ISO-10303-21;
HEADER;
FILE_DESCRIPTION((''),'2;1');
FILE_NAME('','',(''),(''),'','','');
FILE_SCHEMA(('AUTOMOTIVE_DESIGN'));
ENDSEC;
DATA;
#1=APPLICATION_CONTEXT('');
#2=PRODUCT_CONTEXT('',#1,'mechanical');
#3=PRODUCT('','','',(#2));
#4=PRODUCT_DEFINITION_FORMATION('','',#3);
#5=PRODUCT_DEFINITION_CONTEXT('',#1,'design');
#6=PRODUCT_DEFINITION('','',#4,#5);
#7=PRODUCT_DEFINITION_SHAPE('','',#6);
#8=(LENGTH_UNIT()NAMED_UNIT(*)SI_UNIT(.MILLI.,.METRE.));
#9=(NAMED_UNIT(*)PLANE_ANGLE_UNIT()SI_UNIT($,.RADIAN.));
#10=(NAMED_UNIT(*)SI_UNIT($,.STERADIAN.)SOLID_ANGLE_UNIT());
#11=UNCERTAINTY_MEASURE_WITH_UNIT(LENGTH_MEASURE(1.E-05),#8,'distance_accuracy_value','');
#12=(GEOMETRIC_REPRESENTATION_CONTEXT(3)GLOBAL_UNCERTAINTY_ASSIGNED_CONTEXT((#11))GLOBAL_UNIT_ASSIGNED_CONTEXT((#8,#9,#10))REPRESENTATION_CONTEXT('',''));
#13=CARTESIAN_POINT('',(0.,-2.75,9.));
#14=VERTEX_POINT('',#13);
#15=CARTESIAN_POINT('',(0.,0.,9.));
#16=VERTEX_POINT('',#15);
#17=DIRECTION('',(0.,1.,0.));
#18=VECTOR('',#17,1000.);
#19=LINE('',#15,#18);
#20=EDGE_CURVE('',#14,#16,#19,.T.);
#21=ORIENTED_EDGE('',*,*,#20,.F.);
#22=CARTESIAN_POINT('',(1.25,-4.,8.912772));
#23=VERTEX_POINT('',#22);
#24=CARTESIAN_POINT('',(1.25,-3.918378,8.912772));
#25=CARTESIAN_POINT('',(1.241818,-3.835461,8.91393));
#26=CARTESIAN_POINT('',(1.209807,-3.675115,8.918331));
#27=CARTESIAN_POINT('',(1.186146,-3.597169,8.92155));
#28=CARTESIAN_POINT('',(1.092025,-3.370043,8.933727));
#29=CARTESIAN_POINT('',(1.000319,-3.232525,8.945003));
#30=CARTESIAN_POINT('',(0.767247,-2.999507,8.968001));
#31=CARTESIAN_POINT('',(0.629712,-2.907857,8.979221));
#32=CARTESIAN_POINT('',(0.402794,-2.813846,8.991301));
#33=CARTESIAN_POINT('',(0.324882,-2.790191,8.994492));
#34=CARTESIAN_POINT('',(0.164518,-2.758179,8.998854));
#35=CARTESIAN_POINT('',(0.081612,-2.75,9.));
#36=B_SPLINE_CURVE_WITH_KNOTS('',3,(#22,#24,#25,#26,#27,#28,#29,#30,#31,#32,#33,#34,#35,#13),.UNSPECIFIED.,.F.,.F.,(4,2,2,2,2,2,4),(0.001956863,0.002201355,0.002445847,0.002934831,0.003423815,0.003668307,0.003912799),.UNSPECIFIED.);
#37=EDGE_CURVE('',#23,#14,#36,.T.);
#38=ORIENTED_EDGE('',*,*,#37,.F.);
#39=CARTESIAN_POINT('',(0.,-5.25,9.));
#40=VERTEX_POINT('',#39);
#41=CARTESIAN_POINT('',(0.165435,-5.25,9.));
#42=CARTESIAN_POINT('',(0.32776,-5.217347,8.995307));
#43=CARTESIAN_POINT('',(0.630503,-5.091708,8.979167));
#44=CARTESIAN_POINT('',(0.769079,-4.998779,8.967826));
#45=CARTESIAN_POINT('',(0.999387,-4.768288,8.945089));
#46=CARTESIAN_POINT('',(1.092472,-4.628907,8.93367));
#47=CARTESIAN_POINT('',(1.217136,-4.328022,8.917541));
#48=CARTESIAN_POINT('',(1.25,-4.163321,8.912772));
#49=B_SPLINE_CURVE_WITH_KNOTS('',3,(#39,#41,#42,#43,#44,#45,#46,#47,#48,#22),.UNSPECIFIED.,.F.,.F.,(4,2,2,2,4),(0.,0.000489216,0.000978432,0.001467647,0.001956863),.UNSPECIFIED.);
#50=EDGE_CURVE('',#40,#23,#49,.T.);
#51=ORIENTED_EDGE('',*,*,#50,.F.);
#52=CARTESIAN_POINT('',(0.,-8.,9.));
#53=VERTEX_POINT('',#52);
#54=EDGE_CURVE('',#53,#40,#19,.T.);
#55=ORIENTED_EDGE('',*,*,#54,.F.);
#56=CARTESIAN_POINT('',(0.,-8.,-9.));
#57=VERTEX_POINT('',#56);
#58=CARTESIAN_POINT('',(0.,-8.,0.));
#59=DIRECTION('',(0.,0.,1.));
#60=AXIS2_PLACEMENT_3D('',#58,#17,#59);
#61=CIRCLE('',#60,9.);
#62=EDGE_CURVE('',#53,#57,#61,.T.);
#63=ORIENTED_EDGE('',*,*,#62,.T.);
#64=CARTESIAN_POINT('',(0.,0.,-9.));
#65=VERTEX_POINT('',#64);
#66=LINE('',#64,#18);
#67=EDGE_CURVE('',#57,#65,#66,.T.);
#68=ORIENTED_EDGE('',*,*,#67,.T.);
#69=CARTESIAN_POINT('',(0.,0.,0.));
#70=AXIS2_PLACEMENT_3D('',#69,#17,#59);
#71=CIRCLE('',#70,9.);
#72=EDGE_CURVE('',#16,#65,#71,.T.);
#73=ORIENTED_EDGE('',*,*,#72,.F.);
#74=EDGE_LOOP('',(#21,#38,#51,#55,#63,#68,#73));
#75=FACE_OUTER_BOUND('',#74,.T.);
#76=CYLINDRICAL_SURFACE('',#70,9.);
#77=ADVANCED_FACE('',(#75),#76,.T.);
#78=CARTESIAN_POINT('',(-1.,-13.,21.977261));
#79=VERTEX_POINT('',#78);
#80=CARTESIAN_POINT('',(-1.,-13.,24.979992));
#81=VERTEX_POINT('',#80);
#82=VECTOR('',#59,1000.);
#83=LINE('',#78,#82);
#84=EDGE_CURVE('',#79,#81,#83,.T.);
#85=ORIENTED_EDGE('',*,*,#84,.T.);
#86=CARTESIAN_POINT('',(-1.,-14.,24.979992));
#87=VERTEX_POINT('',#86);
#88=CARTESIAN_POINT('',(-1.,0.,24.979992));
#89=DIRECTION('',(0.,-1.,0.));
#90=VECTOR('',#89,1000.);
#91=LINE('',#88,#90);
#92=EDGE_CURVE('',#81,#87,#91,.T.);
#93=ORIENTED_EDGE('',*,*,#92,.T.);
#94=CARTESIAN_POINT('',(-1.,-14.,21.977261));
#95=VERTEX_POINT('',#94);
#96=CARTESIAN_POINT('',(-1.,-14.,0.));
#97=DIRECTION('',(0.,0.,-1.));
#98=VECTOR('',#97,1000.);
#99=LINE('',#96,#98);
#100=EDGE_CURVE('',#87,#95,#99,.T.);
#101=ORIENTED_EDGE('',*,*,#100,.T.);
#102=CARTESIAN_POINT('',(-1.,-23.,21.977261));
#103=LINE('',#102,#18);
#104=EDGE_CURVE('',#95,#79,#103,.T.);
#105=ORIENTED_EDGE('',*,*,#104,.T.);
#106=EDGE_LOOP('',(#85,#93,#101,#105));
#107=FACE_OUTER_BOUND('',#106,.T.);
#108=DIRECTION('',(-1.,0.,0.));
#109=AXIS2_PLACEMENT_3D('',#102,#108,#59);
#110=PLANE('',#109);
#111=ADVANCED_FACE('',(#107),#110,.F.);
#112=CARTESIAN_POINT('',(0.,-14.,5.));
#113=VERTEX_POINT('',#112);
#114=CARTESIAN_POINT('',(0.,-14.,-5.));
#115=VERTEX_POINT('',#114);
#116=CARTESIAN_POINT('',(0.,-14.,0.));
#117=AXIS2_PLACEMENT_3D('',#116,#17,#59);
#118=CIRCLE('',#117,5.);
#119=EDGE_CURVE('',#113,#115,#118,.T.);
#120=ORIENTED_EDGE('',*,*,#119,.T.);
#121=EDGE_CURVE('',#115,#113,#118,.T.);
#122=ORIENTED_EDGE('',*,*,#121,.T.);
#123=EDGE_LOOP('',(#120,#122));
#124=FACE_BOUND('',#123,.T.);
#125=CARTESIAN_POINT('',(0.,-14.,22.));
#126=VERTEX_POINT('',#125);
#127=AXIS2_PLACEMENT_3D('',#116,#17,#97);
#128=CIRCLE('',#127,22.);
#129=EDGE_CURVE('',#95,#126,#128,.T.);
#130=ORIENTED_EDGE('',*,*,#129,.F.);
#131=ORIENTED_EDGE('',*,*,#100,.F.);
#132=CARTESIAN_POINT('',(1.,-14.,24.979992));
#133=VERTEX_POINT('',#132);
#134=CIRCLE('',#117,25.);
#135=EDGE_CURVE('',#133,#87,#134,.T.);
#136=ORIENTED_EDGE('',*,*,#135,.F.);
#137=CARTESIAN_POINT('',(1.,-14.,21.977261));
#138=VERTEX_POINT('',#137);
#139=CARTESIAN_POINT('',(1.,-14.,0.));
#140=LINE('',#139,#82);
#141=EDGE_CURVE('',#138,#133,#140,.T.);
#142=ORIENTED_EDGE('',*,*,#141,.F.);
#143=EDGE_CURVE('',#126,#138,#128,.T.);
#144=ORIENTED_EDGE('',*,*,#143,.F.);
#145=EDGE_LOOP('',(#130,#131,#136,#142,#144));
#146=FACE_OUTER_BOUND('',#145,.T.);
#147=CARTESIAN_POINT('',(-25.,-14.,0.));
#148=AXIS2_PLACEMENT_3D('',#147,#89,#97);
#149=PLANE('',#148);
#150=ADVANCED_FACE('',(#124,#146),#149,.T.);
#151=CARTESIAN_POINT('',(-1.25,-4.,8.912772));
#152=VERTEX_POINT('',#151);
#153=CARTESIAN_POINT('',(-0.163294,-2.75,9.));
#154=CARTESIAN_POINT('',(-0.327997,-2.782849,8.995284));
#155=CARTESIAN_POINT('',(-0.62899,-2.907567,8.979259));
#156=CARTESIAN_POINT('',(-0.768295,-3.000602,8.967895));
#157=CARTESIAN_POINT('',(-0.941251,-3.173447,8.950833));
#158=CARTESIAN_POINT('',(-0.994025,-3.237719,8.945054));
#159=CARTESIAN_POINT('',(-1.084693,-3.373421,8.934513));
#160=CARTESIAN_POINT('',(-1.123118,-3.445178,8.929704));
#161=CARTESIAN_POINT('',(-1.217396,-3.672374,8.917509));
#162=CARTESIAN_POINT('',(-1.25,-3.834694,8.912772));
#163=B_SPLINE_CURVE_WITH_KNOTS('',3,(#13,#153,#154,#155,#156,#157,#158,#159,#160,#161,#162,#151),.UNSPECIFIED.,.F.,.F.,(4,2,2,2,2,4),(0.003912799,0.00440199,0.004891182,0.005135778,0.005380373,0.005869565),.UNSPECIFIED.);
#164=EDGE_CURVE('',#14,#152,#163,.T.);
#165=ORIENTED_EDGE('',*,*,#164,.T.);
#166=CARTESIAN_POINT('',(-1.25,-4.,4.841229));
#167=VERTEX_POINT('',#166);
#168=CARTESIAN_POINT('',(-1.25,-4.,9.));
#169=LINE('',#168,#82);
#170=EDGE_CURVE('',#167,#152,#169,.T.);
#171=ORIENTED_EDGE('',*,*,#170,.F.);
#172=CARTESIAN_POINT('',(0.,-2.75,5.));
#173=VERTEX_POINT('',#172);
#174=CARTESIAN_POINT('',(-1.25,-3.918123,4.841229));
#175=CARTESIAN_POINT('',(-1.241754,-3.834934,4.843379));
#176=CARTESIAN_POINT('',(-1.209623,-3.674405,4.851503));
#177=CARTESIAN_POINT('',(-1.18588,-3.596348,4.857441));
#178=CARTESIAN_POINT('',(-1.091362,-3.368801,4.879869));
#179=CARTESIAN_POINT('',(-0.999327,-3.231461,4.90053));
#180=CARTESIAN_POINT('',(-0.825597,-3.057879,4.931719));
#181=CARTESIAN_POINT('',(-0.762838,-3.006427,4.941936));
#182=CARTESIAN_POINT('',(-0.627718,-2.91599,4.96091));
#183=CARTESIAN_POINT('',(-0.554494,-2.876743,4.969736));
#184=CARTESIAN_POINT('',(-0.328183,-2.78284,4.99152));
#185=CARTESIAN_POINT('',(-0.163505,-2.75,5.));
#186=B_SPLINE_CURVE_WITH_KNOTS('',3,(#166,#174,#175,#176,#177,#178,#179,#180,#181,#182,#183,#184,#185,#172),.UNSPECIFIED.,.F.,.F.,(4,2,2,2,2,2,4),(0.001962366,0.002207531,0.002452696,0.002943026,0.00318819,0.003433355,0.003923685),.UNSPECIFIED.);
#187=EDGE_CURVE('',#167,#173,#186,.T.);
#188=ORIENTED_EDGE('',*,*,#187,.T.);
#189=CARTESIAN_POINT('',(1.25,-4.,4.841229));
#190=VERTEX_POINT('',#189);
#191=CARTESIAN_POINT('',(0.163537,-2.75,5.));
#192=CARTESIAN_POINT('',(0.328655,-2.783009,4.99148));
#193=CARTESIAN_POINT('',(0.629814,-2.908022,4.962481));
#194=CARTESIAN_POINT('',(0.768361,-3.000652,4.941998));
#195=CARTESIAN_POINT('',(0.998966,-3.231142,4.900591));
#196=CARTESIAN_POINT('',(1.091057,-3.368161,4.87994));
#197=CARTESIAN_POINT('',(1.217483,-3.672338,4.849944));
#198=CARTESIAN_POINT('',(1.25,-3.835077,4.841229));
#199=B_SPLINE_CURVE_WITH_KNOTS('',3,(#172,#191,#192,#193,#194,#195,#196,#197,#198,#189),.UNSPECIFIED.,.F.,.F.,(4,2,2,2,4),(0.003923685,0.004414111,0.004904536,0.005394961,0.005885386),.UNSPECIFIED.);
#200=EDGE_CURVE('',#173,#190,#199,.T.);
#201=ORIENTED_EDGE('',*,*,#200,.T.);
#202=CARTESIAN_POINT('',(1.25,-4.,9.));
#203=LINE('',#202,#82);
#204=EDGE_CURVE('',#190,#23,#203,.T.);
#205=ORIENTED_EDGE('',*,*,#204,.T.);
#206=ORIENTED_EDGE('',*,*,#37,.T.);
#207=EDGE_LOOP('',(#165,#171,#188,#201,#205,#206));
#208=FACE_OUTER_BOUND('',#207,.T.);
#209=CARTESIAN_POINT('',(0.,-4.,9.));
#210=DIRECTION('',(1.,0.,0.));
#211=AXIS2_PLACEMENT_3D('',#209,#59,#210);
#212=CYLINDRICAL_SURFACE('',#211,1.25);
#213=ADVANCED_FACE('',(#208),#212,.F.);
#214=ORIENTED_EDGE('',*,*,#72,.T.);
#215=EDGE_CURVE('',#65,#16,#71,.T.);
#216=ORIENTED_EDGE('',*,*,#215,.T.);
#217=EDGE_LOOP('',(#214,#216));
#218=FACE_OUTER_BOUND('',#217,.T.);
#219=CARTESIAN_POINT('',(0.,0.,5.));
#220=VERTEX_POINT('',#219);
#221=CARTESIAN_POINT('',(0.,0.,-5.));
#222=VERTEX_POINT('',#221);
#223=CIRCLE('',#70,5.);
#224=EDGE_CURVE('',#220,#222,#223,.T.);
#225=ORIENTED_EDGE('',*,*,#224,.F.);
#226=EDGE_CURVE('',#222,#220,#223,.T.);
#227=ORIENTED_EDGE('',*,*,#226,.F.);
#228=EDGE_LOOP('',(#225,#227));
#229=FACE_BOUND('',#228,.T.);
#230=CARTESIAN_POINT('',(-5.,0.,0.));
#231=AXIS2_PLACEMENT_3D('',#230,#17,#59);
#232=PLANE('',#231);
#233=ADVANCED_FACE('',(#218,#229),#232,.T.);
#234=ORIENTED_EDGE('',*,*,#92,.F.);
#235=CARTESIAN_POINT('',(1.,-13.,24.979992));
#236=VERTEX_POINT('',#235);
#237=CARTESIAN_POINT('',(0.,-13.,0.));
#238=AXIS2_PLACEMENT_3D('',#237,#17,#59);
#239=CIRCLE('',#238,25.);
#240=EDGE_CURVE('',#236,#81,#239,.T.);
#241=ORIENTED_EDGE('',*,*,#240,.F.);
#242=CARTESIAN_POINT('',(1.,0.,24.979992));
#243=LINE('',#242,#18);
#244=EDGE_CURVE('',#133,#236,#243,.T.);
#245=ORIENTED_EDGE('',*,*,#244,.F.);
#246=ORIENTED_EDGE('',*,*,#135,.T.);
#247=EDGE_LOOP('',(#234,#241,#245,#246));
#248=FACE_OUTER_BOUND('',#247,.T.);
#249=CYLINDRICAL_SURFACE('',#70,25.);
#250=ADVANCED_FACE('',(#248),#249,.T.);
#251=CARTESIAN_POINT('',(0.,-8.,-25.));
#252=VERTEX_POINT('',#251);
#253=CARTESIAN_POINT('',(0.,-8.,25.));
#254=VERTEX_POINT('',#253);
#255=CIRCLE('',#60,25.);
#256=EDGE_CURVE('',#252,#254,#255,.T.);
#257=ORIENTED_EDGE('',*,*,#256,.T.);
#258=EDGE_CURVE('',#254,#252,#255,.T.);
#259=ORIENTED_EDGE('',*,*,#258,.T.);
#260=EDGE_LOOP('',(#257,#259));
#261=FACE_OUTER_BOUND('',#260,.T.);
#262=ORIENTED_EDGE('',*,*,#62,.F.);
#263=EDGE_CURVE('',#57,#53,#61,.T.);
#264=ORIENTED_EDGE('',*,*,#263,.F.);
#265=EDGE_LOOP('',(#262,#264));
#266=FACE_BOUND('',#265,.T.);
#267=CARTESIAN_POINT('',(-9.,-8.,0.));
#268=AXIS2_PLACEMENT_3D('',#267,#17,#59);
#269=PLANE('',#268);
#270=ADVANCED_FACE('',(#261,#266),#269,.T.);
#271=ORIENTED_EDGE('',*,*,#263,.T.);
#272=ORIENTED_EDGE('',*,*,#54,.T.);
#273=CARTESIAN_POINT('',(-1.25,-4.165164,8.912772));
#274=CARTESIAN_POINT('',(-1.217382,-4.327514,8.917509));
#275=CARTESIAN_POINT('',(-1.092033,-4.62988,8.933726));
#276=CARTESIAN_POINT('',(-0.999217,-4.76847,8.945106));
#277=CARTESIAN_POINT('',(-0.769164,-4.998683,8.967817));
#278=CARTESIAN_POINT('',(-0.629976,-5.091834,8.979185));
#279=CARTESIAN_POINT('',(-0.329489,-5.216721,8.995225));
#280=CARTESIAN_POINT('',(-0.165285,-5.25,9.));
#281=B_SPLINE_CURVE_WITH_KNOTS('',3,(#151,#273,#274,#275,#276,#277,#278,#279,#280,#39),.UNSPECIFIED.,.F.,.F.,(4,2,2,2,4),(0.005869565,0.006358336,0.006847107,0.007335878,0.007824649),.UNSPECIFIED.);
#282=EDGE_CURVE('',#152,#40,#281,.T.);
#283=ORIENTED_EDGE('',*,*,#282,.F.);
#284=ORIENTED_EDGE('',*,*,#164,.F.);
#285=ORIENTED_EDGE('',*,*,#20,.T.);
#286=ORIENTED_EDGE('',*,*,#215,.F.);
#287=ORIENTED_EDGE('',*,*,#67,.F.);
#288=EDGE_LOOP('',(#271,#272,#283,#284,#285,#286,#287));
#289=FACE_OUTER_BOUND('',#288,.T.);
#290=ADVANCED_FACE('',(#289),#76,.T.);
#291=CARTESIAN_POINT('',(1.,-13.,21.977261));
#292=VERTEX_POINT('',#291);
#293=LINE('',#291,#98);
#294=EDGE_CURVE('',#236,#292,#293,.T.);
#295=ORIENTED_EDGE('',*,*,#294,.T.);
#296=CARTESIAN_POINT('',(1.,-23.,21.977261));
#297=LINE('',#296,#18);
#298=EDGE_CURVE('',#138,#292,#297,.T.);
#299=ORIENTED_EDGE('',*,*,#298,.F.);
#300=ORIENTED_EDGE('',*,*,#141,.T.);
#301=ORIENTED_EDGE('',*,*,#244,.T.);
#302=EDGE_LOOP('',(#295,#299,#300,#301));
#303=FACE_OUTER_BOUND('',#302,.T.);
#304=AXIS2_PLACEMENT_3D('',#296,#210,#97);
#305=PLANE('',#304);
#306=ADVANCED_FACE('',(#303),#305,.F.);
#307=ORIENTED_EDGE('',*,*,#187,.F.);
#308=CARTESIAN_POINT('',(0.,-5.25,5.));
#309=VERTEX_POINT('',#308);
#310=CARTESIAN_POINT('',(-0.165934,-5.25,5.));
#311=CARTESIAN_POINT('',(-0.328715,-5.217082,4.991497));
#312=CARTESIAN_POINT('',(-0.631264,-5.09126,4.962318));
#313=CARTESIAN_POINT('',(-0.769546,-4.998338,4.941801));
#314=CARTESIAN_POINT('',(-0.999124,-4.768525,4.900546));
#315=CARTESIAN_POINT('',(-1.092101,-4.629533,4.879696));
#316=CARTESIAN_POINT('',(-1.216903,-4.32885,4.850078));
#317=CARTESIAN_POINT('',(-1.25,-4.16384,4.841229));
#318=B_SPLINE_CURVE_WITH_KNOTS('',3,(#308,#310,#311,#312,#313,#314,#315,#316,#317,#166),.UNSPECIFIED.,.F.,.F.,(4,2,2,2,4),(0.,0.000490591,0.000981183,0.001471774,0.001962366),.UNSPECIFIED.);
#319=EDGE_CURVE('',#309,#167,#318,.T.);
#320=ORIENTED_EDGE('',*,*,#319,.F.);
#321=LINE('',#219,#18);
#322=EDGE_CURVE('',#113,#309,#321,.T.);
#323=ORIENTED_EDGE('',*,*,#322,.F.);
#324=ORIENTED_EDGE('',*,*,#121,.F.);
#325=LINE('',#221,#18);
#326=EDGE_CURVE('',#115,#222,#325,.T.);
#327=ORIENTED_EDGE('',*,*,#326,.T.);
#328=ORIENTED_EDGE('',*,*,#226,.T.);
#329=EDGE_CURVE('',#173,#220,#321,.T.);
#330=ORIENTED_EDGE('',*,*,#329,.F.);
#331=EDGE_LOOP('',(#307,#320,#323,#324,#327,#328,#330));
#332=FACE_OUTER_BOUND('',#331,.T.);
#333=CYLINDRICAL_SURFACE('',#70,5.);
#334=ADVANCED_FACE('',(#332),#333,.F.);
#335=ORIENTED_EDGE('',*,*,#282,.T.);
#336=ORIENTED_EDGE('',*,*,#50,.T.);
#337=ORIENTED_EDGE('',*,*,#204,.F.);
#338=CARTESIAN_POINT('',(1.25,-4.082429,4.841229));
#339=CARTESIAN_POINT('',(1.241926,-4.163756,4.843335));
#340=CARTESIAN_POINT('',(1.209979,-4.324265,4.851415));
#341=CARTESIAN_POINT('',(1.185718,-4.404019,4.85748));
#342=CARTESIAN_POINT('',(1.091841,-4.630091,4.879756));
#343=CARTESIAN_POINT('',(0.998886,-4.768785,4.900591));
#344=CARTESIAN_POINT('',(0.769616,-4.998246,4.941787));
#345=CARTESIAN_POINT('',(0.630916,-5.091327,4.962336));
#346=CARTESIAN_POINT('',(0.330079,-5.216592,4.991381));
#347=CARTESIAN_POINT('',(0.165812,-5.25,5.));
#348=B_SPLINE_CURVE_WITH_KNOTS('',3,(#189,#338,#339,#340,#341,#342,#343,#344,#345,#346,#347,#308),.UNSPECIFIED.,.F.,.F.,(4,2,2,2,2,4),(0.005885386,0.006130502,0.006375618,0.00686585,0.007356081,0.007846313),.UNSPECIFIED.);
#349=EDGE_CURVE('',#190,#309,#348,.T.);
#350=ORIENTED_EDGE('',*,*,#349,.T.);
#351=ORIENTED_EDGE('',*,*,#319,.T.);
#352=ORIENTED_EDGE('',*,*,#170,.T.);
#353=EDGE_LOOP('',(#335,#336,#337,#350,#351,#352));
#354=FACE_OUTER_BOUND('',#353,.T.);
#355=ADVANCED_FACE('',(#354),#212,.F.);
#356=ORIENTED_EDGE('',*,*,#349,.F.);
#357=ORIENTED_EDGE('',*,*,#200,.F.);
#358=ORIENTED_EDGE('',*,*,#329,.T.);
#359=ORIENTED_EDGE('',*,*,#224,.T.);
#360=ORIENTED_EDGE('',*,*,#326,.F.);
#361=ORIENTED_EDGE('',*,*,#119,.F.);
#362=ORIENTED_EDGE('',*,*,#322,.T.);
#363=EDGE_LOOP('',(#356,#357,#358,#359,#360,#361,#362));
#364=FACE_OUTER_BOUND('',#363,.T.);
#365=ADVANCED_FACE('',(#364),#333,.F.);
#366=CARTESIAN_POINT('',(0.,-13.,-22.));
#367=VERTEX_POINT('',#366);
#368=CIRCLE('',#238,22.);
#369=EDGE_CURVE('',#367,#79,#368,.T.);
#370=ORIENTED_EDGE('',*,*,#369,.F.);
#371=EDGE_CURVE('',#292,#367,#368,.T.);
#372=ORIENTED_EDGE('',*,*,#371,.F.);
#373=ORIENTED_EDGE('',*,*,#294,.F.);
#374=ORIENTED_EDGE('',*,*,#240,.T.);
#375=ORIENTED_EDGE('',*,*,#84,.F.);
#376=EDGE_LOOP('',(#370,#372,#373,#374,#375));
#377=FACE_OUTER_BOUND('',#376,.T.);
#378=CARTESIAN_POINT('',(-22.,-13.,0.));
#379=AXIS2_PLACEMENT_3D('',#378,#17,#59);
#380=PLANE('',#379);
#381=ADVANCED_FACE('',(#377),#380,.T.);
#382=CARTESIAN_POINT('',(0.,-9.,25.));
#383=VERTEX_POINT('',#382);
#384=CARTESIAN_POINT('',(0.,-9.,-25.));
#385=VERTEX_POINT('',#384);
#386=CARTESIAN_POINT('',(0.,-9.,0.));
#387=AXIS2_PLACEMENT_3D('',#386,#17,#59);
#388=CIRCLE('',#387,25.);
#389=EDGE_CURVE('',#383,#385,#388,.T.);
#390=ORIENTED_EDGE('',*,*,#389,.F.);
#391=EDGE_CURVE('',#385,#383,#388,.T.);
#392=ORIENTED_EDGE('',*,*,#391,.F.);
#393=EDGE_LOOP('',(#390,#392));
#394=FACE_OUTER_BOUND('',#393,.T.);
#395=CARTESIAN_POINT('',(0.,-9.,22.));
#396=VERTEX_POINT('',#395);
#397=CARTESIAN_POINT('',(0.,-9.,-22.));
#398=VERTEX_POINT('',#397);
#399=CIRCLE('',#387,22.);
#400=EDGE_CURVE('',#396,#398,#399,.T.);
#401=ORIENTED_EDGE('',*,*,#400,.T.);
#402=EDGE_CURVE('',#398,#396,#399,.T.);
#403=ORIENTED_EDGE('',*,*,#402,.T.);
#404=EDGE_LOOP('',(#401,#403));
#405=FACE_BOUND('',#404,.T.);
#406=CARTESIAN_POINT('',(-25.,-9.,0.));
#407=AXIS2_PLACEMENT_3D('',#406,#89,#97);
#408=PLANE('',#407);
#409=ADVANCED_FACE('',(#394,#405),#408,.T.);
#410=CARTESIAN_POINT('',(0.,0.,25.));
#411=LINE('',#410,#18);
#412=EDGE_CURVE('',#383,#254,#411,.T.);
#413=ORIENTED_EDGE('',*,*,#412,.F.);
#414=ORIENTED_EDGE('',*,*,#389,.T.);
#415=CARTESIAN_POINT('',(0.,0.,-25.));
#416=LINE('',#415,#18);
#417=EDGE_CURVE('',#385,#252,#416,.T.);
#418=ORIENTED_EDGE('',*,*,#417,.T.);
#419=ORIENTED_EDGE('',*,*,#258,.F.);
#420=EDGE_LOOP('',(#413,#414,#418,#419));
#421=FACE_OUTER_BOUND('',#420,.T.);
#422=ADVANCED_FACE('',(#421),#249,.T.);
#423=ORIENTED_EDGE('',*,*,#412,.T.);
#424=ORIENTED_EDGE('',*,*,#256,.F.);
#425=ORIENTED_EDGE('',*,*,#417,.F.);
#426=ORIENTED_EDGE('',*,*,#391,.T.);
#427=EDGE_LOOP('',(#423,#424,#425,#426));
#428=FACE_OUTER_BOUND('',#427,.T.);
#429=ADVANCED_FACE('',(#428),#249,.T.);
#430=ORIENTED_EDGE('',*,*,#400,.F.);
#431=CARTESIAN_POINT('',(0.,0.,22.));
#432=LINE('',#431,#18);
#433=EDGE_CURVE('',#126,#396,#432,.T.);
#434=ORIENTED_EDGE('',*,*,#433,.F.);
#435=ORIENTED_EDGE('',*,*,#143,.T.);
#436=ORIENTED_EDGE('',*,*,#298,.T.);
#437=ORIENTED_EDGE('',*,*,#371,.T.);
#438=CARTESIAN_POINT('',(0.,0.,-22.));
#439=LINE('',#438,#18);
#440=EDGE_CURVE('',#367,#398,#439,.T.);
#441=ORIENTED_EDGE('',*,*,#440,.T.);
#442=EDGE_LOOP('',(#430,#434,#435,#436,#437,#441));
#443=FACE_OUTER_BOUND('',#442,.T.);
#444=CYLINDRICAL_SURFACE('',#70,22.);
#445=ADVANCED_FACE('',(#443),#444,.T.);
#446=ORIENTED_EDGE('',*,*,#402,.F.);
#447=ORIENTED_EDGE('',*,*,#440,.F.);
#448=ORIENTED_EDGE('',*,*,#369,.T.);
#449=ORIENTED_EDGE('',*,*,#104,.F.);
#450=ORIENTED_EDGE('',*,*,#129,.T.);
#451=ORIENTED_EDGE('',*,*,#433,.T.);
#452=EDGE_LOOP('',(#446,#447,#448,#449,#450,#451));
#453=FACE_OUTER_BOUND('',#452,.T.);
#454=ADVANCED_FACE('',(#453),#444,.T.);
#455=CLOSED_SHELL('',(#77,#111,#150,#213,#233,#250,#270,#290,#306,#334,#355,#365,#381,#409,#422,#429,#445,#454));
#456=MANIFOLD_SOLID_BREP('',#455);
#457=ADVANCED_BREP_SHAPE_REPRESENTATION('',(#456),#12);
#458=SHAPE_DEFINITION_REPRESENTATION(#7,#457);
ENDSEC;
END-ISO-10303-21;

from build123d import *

# Parameters (mm, degrees)
CUT_EXTRUDE1_START    = -10
CUT_EXTRUDE1_DEPTH    = 10
M3_TAPPED_HOLE1_D     = 2.5
M3_TAPPED_HOLE1_DEPTH = 7.5
M3_TAPPED_HOLE1_TIP   = 0.751075774


with BuildPart() as part:
    # Sketch1 → Revolve1 (revolve)
    with BuildSketch(Plane.XY, mode=Mode.PRIVATE) as revolve1_sk:
        Polygon((-5, 0), (-9, 0), (-9, -8), (-25, -8), (-25, -9), (-22, -9), (-22, -13), (-25, -13), (-25, -14), (-5, -14), align=None)
    revolve(revolve1_sk.sketch.rotate(Axis((0, 0, 0), (0, -1, 0)), 270), axis=Axis((0, 0, 0), (0, -1, 0)))

    # Sketch2 → Cut-Extrude1 (cut)
    with BuildSketch(Plane(origin=(0, -13, 0), x_dir=(1, 0, 0), z_dir=(0, 1, 0)).offset(CUT_EXTRUDE1_START)):
        with BuildLine():
            Line((-1, -21.977260976), (-1, -40))
            Line((-1, -40), (1, -40))
            Line((1, -40), (1, -21.977260976))
            ThreePointArc((1, -21.977260976), (0, -22), (-1, -21.977260976))
        make_face()
    extrude(amount=CUT_EXTRUDE1_DEPTH, mode=Mode.SUBTRACT)

    # M3 Tapped Hole1
    with Locations(Plane(origin=(0, -4, 9), x_dir=(1, 0, 0), z_dir=(0, 0, 1))):
        with Locations((0, 0)):
            Hole(M3_TAPPED_HOLE1_D / 2, depth=M3_TAPPED_HOLE1_DEPTH)
            with Locations((0, 0, -(M3_TAPPED_HOLE1_DEPTH + M3_TAPPED_HOLE1_TIP / 2))):  # 118° drill point
                Cone(0, M3_TAPPED_HOLE1_D / 2, M3_TAPPED_HOLE1_TIP, mode=Mode.SUBTRACT)


solid = part.part
